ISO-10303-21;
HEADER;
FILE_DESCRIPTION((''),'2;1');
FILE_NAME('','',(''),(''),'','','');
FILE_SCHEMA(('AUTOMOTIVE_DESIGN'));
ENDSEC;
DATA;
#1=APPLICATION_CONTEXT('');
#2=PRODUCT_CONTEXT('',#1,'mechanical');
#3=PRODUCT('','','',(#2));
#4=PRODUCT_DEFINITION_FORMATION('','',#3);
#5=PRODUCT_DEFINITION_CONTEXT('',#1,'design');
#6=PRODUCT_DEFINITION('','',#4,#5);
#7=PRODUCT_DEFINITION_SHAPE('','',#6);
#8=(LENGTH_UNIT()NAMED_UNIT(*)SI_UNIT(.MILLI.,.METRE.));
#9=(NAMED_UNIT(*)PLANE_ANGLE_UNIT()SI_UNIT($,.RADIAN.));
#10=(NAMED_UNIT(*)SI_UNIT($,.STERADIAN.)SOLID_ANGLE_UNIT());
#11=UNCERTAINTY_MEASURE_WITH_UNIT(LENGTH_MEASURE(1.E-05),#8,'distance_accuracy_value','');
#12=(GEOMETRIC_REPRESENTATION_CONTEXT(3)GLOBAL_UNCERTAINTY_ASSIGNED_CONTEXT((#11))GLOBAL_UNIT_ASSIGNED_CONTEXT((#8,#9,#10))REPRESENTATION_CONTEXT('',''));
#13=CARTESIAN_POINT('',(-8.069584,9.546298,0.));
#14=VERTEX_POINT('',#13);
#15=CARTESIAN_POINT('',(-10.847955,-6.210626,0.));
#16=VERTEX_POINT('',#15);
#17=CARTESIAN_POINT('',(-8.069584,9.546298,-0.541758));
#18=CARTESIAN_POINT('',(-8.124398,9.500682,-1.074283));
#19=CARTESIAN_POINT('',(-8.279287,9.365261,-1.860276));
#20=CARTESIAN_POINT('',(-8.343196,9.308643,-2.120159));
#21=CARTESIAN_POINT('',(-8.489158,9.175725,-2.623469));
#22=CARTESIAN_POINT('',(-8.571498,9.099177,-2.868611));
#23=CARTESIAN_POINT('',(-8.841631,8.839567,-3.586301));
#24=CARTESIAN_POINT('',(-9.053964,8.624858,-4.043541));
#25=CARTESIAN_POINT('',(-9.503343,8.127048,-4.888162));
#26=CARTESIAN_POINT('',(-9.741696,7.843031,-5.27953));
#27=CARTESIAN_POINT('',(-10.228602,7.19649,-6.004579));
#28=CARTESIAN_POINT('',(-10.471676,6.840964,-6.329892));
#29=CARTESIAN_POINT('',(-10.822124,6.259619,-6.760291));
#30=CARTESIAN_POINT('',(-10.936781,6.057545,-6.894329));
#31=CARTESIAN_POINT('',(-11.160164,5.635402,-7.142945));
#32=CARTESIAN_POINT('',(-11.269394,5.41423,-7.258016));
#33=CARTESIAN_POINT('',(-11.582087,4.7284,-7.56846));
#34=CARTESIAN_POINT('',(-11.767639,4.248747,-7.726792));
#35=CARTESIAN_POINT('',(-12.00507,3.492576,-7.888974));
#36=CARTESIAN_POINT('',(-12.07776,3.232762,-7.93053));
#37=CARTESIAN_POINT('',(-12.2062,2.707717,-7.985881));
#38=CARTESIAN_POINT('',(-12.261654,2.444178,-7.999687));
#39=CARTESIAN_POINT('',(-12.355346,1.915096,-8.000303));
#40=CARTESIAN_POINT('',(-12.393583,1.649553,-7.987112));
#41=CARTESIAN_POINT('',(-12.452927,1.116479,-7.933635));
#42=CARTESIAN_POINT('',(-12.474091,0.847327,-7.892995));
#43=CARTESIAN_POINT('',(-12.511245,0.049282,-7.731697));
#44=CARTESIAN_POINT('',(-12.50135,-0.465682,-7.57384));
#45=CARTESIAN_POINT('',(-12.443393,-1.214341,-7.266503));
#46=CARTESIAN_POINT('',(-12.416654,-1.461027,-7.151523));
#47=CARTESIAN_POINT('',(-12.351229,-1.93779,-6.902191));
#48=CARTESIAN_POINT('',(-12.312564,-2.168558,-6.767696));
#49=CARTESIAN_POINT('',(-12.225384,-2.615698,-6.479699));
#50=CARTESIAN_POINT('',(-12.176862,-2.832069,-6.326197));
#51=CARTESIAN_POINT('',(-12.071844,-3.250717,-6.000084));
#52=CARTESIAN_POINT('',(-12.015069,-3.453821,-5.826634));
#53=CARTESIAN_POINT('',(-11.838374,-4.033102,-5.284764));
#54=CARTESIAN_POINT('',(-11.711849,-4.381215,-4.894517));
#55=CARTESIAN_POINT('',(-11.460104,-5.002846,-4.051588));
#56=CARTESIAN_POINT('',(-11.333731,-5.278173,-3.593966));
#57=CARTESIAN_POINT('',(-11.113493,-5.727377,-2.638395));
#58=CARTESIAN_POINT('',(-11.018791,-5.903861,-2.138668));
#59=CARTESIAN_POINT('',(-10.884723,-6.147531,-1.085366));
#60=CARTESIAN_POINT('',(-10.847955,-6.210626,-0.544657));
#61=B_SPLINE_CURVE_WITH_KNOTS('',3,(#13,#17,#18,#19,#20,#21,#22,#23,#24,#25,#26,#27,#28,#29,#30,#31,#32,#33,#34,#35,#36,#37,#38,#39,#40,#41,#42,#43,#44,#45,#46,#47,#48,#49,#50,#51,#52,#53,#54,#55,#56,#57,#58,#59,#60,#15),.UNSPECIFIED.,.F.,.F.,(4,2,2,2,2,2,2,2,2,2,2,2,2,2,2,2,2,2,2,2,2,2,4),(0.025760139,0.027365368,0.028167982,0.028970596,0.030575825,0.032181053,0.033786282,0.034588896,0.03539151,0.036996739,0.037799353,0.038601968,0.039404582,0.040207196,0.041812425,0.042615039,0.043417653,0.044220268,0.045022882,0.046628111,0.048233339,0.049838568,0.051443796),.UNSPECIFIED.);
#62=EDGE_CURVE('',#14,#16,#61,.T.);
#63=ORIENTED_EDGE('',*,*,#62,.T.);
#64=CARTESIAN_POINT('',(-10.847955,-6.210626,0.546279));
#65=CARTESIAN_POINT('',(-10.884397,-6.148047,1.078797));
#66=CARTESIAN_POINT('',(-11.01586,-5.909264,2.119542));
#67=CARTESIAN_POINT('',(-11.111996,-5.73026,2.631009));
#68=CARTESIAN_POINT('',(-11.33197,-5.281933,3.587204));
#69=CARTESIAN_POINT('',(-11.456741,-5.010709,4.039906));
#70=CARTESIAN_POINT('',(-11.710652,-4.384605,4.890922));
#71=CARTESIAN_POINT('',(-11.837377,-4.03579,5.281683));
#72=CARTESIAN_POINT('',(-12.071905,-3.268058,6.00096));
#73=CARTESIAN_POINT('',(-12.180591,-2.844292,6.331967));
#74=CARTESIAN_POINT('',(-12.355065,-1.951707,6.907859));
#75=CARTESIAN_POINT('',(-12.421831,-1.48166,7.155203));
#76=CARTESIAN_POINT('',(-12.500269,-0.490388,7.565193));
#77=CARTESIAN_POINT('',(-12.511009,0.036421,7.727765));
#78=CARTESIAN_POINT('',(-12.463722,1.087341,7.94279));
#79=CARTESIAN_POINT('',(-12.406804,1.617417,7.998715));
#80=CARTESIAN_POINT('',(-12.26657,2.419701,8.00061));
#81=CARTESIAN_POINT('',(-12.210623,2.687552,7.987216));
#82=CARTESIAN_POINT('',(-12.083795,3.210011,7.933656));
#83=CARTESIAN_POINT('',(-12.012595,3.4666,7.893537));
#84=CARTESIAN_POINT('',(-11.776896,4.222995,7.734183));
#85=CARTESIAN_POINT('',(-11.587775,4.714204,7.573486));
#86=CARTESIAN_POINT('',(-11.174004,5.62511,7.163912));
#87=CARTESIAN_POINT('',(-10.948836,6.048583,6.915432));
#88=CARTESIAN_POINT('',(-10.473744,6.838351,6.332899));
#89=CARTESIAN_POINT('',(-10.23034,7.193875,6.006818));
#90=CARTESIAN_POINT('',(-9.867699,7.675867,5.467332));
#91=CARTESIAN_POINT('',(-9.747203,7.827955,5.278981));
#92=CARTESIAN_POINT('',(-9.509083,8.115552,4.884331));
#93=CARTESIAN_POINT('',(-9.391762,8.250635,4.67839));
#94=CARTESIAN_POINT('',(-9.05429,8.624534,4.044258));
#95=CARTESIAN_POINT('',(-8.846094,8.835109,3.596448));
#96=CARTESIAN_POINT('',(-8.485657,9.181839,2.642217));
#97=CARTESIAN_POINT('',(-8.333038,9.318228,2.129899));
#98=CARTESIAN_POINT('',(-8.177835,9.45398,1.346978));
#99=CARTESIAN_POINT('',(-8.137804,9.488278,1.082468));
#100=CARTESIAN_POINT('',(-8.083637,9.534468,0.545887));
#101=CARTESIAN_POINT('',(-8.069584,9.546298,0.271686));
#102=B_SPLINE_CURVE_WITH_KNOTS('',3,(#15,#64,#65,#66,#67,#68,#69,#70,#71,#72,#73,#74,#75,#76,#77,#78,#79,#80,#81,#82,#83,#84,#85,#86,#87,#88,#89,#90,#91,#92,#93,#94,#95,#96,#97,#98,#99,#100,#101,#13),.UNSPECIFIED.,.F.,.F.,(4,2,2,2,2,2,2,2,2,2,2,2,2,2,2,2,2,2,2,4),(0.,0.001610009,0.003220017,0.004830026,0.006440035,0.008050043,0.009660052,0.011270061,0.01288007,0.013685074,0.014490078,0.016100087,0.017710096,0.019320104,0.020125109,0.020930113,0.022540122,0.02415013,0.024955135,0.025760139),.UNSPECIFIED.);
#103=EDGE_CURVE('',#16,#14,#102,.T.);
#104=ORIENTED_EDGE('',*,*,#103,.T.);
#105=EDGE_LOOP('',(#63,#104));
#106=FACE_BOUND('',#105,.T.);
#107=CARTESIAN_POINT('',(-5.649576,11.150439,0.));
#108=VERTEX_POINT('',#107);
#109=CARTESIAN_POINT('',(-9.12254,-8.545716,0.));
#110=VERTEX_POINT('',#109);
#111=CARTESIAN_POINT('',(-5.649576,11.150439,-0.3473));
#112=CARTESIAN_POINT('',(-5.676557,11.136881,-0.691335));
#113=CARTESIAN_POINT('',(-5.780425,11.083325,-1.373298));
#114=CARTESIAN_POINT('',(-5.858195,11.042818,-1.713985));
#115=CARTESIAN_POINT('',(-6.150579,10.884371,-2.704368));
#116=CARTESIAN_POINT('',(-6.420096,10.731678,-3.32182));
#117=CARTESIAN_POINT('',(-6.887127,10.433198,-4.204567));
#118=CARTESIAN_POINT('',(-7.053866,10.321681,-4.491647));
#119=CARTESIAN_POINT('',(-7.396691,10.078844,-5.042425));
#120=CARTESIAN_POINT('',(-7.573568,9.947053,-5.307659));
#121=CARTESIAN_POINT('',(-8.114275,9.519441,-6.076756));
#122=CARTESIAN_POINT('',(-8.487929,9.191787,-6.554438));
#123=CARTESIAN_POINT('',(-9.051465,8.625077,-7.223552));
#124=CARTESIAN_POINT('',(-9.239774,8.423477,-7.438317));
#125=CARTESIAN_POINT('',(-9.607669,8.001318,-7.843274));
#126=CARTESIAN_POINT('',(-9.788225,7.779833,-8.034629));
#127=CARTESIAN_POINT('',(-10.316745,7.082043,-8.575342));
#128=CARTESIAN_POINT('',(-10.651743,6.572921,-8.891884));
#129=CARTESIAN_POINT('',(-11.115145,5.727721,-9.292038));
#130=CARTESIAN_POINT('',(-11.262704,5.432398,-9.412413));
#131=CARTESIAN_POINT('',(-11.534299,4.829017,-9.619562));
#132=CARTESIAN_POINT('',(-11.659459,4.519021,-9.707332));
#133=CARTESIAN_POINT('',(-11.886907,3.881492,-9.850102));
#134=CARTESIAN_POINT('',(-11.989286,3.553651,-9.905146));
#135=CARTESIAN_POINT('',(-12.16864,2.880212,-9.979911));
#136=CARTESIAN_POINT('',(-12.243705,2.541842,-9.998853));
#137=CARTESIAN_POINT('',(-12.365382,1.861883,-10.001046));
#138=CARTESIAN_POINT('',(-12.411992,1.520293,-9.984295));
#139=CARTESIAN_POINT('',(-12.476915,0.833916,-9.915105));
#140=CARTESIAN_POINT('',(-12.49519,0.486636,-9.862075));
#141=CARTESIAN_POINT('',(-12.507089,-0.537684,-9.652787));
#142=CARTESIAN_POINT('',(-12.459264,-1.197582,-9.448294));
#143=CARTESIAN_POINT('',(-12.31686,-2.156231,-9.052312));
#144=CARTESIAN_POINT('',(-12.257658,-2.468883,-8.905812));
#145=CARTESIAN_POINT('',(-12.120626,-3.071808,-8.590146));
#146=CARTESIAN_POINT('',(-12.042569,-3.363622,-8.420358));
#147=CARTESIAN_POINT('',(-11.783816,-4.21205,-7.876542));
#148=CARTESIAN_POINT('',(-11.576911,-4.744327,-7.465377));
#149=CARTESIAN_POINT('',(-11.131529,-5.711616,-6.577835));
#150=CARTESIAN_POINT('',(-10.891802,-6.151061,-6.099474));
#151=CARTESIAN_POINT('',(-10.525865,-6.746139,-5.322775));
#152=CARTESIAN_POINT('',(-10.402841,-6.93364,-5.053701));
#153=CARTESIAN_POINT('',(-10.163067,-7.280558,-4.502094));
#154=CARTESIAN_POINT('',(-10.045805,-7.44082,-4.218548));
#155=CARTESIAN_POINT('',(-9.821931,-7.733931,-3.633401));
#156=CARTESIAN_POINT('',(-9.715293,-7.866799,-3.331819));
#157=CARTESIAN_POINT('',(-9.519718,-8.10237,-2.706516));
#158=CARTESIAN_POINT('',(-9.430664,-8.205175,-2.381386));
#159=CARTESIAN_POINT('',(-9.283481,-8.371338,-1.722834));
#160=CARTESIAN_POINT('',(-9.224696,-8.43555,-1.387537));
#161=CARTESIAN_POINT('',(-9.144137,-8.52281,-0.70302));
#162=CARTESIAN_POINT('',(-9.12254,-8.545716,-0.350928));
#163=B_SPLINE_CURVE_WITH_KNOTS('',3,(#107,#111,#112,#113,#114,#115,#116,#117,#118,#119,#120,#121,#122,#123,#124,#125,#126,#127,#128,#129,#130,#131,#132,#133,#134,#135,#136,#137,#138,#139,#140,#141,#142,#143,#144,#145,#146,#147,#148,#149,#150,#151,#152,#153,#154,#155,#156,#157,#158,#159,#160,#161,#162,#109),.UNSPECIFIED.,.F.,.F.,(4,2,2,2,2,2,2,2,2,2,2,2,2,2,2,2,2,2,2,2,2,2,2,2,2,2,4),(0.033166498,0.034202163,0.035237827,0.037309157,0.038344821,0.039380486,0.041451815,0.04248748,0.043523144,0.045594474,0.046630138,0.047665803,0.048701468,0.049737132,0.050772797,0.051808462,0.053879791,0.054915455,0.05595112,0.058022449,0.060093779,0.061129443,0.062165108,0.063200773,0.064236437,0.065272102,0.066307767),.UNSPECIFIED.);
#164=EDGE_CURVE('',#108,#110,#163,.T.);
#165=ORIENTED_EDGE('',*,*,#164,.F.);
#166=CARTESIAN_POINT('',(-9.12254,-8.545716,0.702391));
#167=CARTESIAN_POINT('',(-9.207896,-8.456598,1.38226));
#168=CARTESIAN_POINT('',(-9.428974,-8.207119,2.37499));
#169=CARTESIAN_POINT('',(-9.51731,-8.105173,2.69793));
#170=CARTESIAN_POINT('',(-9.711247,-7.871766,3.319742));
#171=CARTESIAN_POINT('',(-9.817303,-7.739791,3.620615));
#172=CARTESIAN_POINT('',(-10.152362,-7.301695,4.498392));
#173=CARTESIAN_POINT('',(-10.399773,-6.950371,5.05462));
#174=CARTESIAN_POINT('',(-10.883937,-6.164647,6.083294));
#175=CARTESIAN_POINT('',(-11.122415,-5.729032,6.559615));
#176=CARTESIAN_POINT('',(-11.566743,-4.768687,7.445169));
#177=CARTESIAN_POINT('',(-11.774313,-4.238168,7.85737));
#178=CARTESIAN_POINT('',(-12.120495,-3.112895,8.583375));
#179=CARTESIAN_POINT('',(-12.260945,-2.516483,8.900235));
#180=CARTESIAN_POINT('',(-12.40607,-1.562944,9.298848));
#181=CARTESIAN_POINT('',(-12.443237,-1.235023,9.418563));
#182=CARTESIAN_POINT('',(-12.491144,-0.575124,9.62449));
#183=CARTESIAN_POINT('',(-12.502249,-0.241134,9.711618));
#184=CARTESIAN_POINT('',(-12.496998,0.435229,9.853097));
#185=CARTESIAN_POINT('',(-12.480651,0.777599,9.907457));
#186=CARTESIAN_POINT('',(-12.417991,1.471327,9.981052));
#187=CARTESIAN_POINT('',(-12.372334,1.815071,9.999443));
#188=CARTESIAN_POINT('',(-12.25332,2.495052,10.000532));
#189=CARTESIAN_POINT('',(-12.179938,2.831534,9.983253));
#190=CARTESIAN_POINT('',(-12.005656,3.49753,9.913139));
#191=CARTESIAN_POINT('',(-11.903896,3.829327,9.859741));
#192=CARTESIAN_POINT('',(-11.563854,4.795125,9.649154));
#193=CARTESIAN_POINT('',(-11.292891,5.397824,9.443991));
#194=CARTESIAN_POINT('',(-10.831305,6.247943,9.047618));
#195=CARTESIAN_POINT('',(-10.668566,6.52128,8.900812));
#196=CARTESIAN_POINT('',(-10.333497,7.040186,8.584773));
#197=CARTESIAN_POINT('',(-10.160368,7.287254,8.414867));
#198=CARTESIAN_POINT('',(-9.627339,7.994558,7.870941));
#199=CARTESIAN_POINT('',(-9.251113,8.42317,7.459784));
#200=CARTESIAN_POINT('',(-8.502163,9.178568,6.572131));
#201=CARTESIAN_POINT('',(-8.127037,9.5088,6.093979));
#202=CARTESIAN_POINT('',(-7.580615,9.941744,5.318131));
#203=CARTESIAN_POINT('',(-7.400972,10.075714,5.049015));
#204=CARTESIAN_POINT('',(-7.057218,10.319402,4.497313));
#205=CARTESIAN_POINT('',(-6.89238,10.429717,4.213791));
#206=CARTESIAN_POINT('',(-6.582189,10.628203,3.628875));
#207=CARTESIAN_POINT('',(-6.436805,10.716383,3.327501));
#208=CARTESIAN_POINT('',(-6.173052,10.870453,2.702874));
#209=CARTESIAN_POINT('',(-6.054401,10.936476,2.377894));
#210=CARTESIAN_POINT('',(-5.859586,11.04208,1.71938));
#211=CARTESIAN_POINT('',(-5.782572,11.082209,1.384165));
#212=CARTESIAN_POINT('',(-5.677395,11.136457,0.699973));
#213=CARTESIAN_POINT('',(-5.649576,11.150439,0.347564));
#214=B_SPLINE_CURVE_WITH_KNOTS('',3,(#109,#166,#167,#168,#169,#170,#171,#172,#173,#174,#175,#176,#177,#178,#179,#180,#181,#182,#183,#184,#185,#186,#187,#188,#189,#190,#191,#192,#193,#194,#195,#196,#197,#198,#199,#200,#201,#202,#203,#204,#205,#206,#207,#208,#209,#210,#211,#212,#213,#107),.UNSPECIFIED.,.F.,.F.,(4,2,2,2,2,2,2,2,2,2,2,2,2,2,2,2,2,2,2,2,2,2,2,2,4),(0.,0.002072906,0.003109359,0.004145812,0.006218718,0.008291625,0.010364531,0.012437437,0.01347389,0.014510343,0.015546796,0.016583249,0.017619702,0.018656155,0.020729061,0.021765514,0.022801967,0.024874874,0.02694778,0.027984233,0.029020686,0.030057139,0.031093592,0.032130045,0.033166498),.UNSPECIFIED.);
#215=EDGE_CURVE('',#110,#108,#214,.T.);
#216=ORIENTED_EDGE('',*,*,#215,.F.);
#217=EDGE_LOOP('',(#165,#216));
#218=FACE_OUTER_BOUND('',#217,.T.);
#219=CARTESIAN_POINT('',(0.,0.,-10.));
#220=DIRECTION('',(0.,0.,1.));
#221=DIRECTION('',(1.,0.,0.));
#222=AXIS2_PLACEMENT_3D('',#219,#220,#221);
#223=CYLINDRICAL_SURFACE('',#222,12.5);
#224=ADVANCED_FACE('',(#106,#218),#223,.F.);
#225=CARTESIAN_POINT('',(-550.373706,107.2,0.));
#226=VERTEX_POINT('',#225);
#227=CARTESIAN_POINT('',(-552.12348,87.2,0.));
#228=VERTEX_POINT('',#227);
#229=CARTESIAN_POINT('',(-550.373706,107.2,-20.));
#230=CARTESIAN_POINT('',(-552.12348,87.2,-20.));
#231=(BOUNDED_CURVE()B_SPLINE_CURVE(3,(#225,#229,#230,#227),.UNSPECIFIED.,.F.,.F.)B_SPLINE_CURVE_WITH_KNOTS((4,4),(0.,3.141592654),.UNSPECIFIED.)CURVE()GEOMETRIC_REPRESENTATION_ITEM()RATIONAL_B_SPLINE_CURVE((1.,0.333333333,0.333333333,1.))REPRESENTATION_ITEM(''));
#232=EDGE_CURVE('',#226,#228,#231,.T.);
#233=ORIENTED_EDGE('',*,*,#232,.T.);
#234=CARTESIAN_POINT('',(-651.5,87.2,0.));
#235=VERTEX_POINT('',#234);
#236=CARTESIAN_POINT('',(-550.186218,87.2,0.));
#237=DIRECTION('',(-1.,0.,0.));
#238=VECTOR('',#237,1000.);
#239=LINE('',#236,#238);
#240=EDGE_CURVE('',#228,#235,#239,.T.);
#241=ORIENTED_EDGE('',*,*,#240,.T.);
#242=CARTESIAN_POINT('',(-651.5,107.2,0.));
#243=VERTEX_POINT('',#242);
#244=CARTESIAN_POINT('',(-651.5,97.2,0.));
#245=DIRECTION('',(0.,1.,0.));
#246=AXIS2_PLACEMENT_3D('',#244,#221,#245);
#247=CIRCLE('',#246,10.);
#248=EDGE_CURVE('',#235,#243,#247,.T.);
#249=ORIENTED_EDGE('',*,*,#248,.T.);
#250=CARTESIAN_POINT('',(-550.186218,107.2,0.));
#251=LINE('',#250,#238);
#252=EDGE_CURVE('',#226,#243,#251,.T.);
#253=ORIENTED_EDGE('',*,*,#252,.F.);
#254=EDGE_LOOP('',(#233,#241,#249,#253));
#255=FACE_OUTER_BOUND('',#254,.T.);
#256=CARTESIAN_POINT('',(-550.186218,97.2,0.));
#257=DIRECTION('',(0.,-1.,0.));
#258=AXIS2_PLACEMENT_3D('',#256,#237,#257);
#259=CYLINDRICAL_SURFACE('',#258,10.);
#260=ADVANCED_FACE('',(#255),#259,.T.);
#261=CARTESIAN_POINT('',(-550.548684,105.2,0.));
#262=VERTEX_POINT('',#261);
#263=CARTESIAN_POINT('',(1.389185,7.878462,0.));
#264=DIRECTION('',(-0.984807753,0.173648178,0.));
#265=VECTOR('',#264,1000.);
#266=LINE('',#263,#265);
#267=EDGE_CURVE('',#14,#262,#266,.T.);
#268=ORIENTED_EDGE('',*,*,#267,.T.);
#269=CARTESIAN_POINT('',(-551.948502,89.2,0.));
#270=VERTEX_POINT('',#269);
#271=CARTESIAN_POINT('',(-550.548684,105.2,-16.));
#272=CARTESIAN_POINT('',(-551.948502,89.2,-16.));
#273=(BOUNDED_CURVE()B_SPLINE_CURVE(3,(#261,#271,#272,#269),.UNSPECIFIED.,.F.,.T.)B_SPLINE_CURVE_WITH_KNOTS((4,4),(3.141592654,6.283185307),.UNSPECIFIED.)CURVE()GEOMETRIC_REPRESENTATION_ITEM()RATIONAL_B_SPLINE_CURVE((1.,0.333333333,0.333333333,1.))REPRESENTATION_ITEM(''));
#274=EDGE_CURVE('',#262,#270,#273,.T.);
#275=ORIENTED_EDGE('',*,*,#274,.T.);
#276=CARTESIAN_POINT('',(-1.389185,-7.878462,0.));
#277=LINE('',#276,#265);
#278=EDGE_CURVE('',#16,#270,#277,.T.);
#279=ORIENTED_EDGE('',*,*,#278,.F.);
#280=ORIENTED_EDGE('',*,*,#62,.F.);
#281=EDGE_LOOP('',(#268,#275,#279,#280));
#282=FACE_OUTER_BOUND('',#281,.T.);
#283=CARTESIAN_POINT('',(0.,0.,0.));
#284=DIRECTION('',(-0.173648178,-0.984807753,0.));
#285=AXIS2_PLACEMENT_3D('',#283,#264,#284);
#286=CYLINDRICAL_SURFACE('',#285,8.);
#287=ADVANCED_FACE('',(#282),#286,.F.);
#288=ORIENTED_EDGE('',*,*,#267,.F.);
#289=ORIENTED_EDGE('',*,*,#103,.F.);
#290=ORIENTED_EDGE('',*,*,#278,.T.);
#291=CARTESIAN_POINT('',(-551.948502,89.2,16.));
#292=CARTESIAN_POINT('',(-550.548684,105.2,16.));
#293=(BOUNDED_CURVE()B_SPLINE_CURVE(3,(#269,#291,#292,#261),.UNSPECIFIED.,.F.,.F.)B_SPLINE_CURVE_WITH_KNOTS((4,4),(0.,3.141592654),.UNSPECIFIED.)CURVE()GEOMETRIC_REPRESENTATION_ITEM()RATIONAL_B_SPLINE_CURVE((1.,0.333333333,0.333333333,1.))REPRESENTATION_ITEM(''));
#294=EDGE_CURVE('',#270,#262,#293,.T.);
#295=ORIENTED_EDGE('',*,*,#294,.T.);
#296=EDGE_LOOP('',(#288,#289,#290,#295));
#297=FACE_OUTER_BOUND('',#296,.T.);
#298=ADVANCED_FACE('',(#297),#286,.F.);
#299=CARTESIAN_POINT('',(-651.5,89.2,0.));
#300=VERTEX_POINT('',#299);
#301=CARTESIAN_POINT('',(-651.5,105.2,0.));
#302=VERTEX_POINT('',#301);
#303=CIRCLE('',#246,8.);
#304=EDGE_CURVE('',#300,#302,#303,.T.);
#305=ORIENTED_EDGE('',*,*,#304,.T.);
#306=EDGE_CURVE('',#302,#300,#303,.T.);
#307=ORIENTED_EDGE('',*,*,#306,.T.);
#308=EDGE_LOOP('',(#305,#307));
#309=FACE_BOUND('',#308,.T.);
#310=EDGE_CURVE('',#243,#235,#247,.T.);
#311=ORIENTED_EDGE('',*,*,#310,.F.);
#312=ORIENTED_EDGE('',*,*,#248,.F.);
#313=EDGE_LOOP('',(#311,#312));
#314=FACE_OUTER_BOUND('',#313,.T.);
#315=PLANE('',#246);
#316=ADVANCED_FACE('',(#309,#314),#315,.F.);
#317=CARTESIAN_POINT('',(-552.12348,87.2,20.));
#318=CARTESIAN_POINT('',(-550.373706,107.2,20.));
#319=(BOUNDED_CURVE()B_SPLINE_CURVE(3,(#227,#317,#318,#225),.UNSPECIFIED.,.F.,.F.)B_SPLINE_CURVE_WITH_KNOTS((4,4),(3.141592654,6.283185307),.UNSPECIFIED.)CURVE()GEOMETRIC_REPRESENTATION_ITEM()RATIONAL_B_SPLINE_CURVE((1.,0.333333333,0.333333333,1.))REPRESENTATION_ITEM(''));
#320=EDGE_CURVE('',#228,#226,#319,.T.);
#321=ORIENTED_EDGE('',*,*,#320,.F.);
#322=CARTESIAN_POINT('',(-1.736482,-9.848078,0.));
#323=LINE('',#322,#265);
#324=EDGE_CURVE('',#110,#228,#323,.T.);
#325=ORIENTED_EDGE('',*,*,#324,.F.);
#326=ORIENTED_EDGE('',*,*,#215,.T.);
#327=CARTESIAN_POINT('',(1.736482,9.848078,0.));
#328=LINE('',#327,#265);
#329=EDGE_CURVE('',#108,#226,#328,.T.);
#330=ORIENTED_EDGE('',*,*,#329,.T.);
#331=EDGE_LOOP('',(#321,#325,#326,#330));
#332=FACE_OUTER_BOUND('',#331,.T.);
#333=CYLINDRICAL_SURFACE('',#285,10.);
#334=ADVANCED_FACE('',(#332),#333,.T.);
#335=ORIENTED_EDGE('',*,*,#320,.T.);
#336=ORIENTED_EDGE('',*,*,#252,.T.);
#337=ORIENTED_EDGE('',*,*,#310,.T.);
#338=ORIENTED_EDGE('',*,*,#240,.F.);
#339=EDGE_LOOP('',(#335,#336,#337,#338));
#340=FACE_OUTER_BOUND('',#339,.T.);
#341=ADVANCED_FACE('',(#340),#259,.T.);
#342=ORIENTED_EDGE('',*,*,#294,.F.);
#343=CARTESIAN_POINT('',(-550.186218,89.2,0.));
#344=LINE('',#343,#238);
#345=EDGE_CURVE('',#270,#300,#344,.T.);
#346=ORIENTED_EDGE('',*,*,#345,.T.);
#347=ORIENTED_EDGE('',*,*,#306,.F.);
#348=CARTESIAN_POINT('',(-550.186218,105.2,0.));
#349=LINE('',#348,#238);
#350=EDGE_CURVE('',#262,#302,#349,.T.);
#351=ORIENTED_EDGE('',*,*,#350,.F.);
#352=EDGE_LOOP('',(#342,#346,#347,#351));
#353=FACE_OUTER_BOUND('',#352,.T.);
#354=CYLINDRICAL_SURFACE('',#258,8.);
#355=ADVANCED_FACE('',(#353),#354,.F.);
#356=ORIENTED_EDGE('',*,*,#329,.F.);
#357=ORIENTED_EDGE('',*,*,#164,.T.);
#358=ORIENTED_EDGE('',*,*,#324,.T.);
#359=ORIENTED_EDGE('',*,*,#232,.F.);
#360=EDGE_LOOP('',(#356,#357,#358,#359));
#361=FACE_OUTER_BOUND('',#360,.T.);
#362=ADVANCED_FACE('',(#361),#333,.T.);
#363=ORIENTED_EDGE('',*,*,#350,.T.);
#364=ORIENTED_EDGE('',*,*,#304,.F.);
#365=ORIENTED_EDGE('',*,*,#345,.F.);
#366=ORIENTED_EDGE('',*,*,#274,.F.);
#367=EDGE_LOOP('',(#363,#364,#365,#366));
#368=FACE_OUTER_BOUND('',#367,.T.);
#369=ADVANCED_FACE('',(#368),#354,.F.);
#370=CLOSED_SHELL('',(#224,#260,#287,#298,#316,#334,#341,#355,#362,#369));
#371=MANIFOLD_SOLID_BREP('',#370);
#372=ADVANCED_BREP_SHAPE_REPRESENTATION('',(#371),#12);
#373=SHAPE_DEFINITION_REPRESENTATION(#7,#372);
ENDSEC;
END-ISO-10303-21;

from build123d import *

# Parameters (mm, degrees)
SWEEP_THIN_1_PROFILE_R   = 10
SWEEP_THIN_1_PROFILE_R_2 = 8
CUT_EXTRUDE1_DEPTH       = 661.336346115
CUT_EXTRUDE1_DEPTH_BACK  = 661.336346115
SKETCH12_R               = 12.5


with BuildPart() as part:
    # Sweep-thin 1: sweep along a path in Sketch1
    with BuildLine(Plane.XY) as sweep_thin_1_path:
        Line((0, 0), (-551.248592867, 97.2))
        Line((-551.248592867, 97.2), (-651.5, 97.2))
    # Sweep-thin 1 profile (on start of the path) → Sweep-thin 1 (sweep)
    with BuildSketch(Plane(origin=(0, 0, 0), x_dir=(-0.1736481776669304, -0.9848077530122081, 0), z_dir=(-0.9848077530122081, 0.1736481776669304, 0))):
        Circle(SWEEP_THIN_1_PROFILE_R)
        Circle(SWEEP_THIN_1_PROFILE_R_2, mode=Mode.SUBTRACT)
    sweep(path=sweep_thin_1_path.line, transition=Transition.RIGHT)

    # Sketch12 → Cut-Extrude1 (cut, two sides: drawn at the far end of the back side and taken through both)
    with BuildSketch(Plane.XY.offset(-CUT_EXTRUDE1_DEPTH_BACK)):
        Circle(SKETCH12_R)
    extrude(amount=CUT_EXTRUDE1_DEPTH + CUT_EXTRUDE1_DEPTH_BACK, mode=Mode.SUBTRACT)


solid = part.part
